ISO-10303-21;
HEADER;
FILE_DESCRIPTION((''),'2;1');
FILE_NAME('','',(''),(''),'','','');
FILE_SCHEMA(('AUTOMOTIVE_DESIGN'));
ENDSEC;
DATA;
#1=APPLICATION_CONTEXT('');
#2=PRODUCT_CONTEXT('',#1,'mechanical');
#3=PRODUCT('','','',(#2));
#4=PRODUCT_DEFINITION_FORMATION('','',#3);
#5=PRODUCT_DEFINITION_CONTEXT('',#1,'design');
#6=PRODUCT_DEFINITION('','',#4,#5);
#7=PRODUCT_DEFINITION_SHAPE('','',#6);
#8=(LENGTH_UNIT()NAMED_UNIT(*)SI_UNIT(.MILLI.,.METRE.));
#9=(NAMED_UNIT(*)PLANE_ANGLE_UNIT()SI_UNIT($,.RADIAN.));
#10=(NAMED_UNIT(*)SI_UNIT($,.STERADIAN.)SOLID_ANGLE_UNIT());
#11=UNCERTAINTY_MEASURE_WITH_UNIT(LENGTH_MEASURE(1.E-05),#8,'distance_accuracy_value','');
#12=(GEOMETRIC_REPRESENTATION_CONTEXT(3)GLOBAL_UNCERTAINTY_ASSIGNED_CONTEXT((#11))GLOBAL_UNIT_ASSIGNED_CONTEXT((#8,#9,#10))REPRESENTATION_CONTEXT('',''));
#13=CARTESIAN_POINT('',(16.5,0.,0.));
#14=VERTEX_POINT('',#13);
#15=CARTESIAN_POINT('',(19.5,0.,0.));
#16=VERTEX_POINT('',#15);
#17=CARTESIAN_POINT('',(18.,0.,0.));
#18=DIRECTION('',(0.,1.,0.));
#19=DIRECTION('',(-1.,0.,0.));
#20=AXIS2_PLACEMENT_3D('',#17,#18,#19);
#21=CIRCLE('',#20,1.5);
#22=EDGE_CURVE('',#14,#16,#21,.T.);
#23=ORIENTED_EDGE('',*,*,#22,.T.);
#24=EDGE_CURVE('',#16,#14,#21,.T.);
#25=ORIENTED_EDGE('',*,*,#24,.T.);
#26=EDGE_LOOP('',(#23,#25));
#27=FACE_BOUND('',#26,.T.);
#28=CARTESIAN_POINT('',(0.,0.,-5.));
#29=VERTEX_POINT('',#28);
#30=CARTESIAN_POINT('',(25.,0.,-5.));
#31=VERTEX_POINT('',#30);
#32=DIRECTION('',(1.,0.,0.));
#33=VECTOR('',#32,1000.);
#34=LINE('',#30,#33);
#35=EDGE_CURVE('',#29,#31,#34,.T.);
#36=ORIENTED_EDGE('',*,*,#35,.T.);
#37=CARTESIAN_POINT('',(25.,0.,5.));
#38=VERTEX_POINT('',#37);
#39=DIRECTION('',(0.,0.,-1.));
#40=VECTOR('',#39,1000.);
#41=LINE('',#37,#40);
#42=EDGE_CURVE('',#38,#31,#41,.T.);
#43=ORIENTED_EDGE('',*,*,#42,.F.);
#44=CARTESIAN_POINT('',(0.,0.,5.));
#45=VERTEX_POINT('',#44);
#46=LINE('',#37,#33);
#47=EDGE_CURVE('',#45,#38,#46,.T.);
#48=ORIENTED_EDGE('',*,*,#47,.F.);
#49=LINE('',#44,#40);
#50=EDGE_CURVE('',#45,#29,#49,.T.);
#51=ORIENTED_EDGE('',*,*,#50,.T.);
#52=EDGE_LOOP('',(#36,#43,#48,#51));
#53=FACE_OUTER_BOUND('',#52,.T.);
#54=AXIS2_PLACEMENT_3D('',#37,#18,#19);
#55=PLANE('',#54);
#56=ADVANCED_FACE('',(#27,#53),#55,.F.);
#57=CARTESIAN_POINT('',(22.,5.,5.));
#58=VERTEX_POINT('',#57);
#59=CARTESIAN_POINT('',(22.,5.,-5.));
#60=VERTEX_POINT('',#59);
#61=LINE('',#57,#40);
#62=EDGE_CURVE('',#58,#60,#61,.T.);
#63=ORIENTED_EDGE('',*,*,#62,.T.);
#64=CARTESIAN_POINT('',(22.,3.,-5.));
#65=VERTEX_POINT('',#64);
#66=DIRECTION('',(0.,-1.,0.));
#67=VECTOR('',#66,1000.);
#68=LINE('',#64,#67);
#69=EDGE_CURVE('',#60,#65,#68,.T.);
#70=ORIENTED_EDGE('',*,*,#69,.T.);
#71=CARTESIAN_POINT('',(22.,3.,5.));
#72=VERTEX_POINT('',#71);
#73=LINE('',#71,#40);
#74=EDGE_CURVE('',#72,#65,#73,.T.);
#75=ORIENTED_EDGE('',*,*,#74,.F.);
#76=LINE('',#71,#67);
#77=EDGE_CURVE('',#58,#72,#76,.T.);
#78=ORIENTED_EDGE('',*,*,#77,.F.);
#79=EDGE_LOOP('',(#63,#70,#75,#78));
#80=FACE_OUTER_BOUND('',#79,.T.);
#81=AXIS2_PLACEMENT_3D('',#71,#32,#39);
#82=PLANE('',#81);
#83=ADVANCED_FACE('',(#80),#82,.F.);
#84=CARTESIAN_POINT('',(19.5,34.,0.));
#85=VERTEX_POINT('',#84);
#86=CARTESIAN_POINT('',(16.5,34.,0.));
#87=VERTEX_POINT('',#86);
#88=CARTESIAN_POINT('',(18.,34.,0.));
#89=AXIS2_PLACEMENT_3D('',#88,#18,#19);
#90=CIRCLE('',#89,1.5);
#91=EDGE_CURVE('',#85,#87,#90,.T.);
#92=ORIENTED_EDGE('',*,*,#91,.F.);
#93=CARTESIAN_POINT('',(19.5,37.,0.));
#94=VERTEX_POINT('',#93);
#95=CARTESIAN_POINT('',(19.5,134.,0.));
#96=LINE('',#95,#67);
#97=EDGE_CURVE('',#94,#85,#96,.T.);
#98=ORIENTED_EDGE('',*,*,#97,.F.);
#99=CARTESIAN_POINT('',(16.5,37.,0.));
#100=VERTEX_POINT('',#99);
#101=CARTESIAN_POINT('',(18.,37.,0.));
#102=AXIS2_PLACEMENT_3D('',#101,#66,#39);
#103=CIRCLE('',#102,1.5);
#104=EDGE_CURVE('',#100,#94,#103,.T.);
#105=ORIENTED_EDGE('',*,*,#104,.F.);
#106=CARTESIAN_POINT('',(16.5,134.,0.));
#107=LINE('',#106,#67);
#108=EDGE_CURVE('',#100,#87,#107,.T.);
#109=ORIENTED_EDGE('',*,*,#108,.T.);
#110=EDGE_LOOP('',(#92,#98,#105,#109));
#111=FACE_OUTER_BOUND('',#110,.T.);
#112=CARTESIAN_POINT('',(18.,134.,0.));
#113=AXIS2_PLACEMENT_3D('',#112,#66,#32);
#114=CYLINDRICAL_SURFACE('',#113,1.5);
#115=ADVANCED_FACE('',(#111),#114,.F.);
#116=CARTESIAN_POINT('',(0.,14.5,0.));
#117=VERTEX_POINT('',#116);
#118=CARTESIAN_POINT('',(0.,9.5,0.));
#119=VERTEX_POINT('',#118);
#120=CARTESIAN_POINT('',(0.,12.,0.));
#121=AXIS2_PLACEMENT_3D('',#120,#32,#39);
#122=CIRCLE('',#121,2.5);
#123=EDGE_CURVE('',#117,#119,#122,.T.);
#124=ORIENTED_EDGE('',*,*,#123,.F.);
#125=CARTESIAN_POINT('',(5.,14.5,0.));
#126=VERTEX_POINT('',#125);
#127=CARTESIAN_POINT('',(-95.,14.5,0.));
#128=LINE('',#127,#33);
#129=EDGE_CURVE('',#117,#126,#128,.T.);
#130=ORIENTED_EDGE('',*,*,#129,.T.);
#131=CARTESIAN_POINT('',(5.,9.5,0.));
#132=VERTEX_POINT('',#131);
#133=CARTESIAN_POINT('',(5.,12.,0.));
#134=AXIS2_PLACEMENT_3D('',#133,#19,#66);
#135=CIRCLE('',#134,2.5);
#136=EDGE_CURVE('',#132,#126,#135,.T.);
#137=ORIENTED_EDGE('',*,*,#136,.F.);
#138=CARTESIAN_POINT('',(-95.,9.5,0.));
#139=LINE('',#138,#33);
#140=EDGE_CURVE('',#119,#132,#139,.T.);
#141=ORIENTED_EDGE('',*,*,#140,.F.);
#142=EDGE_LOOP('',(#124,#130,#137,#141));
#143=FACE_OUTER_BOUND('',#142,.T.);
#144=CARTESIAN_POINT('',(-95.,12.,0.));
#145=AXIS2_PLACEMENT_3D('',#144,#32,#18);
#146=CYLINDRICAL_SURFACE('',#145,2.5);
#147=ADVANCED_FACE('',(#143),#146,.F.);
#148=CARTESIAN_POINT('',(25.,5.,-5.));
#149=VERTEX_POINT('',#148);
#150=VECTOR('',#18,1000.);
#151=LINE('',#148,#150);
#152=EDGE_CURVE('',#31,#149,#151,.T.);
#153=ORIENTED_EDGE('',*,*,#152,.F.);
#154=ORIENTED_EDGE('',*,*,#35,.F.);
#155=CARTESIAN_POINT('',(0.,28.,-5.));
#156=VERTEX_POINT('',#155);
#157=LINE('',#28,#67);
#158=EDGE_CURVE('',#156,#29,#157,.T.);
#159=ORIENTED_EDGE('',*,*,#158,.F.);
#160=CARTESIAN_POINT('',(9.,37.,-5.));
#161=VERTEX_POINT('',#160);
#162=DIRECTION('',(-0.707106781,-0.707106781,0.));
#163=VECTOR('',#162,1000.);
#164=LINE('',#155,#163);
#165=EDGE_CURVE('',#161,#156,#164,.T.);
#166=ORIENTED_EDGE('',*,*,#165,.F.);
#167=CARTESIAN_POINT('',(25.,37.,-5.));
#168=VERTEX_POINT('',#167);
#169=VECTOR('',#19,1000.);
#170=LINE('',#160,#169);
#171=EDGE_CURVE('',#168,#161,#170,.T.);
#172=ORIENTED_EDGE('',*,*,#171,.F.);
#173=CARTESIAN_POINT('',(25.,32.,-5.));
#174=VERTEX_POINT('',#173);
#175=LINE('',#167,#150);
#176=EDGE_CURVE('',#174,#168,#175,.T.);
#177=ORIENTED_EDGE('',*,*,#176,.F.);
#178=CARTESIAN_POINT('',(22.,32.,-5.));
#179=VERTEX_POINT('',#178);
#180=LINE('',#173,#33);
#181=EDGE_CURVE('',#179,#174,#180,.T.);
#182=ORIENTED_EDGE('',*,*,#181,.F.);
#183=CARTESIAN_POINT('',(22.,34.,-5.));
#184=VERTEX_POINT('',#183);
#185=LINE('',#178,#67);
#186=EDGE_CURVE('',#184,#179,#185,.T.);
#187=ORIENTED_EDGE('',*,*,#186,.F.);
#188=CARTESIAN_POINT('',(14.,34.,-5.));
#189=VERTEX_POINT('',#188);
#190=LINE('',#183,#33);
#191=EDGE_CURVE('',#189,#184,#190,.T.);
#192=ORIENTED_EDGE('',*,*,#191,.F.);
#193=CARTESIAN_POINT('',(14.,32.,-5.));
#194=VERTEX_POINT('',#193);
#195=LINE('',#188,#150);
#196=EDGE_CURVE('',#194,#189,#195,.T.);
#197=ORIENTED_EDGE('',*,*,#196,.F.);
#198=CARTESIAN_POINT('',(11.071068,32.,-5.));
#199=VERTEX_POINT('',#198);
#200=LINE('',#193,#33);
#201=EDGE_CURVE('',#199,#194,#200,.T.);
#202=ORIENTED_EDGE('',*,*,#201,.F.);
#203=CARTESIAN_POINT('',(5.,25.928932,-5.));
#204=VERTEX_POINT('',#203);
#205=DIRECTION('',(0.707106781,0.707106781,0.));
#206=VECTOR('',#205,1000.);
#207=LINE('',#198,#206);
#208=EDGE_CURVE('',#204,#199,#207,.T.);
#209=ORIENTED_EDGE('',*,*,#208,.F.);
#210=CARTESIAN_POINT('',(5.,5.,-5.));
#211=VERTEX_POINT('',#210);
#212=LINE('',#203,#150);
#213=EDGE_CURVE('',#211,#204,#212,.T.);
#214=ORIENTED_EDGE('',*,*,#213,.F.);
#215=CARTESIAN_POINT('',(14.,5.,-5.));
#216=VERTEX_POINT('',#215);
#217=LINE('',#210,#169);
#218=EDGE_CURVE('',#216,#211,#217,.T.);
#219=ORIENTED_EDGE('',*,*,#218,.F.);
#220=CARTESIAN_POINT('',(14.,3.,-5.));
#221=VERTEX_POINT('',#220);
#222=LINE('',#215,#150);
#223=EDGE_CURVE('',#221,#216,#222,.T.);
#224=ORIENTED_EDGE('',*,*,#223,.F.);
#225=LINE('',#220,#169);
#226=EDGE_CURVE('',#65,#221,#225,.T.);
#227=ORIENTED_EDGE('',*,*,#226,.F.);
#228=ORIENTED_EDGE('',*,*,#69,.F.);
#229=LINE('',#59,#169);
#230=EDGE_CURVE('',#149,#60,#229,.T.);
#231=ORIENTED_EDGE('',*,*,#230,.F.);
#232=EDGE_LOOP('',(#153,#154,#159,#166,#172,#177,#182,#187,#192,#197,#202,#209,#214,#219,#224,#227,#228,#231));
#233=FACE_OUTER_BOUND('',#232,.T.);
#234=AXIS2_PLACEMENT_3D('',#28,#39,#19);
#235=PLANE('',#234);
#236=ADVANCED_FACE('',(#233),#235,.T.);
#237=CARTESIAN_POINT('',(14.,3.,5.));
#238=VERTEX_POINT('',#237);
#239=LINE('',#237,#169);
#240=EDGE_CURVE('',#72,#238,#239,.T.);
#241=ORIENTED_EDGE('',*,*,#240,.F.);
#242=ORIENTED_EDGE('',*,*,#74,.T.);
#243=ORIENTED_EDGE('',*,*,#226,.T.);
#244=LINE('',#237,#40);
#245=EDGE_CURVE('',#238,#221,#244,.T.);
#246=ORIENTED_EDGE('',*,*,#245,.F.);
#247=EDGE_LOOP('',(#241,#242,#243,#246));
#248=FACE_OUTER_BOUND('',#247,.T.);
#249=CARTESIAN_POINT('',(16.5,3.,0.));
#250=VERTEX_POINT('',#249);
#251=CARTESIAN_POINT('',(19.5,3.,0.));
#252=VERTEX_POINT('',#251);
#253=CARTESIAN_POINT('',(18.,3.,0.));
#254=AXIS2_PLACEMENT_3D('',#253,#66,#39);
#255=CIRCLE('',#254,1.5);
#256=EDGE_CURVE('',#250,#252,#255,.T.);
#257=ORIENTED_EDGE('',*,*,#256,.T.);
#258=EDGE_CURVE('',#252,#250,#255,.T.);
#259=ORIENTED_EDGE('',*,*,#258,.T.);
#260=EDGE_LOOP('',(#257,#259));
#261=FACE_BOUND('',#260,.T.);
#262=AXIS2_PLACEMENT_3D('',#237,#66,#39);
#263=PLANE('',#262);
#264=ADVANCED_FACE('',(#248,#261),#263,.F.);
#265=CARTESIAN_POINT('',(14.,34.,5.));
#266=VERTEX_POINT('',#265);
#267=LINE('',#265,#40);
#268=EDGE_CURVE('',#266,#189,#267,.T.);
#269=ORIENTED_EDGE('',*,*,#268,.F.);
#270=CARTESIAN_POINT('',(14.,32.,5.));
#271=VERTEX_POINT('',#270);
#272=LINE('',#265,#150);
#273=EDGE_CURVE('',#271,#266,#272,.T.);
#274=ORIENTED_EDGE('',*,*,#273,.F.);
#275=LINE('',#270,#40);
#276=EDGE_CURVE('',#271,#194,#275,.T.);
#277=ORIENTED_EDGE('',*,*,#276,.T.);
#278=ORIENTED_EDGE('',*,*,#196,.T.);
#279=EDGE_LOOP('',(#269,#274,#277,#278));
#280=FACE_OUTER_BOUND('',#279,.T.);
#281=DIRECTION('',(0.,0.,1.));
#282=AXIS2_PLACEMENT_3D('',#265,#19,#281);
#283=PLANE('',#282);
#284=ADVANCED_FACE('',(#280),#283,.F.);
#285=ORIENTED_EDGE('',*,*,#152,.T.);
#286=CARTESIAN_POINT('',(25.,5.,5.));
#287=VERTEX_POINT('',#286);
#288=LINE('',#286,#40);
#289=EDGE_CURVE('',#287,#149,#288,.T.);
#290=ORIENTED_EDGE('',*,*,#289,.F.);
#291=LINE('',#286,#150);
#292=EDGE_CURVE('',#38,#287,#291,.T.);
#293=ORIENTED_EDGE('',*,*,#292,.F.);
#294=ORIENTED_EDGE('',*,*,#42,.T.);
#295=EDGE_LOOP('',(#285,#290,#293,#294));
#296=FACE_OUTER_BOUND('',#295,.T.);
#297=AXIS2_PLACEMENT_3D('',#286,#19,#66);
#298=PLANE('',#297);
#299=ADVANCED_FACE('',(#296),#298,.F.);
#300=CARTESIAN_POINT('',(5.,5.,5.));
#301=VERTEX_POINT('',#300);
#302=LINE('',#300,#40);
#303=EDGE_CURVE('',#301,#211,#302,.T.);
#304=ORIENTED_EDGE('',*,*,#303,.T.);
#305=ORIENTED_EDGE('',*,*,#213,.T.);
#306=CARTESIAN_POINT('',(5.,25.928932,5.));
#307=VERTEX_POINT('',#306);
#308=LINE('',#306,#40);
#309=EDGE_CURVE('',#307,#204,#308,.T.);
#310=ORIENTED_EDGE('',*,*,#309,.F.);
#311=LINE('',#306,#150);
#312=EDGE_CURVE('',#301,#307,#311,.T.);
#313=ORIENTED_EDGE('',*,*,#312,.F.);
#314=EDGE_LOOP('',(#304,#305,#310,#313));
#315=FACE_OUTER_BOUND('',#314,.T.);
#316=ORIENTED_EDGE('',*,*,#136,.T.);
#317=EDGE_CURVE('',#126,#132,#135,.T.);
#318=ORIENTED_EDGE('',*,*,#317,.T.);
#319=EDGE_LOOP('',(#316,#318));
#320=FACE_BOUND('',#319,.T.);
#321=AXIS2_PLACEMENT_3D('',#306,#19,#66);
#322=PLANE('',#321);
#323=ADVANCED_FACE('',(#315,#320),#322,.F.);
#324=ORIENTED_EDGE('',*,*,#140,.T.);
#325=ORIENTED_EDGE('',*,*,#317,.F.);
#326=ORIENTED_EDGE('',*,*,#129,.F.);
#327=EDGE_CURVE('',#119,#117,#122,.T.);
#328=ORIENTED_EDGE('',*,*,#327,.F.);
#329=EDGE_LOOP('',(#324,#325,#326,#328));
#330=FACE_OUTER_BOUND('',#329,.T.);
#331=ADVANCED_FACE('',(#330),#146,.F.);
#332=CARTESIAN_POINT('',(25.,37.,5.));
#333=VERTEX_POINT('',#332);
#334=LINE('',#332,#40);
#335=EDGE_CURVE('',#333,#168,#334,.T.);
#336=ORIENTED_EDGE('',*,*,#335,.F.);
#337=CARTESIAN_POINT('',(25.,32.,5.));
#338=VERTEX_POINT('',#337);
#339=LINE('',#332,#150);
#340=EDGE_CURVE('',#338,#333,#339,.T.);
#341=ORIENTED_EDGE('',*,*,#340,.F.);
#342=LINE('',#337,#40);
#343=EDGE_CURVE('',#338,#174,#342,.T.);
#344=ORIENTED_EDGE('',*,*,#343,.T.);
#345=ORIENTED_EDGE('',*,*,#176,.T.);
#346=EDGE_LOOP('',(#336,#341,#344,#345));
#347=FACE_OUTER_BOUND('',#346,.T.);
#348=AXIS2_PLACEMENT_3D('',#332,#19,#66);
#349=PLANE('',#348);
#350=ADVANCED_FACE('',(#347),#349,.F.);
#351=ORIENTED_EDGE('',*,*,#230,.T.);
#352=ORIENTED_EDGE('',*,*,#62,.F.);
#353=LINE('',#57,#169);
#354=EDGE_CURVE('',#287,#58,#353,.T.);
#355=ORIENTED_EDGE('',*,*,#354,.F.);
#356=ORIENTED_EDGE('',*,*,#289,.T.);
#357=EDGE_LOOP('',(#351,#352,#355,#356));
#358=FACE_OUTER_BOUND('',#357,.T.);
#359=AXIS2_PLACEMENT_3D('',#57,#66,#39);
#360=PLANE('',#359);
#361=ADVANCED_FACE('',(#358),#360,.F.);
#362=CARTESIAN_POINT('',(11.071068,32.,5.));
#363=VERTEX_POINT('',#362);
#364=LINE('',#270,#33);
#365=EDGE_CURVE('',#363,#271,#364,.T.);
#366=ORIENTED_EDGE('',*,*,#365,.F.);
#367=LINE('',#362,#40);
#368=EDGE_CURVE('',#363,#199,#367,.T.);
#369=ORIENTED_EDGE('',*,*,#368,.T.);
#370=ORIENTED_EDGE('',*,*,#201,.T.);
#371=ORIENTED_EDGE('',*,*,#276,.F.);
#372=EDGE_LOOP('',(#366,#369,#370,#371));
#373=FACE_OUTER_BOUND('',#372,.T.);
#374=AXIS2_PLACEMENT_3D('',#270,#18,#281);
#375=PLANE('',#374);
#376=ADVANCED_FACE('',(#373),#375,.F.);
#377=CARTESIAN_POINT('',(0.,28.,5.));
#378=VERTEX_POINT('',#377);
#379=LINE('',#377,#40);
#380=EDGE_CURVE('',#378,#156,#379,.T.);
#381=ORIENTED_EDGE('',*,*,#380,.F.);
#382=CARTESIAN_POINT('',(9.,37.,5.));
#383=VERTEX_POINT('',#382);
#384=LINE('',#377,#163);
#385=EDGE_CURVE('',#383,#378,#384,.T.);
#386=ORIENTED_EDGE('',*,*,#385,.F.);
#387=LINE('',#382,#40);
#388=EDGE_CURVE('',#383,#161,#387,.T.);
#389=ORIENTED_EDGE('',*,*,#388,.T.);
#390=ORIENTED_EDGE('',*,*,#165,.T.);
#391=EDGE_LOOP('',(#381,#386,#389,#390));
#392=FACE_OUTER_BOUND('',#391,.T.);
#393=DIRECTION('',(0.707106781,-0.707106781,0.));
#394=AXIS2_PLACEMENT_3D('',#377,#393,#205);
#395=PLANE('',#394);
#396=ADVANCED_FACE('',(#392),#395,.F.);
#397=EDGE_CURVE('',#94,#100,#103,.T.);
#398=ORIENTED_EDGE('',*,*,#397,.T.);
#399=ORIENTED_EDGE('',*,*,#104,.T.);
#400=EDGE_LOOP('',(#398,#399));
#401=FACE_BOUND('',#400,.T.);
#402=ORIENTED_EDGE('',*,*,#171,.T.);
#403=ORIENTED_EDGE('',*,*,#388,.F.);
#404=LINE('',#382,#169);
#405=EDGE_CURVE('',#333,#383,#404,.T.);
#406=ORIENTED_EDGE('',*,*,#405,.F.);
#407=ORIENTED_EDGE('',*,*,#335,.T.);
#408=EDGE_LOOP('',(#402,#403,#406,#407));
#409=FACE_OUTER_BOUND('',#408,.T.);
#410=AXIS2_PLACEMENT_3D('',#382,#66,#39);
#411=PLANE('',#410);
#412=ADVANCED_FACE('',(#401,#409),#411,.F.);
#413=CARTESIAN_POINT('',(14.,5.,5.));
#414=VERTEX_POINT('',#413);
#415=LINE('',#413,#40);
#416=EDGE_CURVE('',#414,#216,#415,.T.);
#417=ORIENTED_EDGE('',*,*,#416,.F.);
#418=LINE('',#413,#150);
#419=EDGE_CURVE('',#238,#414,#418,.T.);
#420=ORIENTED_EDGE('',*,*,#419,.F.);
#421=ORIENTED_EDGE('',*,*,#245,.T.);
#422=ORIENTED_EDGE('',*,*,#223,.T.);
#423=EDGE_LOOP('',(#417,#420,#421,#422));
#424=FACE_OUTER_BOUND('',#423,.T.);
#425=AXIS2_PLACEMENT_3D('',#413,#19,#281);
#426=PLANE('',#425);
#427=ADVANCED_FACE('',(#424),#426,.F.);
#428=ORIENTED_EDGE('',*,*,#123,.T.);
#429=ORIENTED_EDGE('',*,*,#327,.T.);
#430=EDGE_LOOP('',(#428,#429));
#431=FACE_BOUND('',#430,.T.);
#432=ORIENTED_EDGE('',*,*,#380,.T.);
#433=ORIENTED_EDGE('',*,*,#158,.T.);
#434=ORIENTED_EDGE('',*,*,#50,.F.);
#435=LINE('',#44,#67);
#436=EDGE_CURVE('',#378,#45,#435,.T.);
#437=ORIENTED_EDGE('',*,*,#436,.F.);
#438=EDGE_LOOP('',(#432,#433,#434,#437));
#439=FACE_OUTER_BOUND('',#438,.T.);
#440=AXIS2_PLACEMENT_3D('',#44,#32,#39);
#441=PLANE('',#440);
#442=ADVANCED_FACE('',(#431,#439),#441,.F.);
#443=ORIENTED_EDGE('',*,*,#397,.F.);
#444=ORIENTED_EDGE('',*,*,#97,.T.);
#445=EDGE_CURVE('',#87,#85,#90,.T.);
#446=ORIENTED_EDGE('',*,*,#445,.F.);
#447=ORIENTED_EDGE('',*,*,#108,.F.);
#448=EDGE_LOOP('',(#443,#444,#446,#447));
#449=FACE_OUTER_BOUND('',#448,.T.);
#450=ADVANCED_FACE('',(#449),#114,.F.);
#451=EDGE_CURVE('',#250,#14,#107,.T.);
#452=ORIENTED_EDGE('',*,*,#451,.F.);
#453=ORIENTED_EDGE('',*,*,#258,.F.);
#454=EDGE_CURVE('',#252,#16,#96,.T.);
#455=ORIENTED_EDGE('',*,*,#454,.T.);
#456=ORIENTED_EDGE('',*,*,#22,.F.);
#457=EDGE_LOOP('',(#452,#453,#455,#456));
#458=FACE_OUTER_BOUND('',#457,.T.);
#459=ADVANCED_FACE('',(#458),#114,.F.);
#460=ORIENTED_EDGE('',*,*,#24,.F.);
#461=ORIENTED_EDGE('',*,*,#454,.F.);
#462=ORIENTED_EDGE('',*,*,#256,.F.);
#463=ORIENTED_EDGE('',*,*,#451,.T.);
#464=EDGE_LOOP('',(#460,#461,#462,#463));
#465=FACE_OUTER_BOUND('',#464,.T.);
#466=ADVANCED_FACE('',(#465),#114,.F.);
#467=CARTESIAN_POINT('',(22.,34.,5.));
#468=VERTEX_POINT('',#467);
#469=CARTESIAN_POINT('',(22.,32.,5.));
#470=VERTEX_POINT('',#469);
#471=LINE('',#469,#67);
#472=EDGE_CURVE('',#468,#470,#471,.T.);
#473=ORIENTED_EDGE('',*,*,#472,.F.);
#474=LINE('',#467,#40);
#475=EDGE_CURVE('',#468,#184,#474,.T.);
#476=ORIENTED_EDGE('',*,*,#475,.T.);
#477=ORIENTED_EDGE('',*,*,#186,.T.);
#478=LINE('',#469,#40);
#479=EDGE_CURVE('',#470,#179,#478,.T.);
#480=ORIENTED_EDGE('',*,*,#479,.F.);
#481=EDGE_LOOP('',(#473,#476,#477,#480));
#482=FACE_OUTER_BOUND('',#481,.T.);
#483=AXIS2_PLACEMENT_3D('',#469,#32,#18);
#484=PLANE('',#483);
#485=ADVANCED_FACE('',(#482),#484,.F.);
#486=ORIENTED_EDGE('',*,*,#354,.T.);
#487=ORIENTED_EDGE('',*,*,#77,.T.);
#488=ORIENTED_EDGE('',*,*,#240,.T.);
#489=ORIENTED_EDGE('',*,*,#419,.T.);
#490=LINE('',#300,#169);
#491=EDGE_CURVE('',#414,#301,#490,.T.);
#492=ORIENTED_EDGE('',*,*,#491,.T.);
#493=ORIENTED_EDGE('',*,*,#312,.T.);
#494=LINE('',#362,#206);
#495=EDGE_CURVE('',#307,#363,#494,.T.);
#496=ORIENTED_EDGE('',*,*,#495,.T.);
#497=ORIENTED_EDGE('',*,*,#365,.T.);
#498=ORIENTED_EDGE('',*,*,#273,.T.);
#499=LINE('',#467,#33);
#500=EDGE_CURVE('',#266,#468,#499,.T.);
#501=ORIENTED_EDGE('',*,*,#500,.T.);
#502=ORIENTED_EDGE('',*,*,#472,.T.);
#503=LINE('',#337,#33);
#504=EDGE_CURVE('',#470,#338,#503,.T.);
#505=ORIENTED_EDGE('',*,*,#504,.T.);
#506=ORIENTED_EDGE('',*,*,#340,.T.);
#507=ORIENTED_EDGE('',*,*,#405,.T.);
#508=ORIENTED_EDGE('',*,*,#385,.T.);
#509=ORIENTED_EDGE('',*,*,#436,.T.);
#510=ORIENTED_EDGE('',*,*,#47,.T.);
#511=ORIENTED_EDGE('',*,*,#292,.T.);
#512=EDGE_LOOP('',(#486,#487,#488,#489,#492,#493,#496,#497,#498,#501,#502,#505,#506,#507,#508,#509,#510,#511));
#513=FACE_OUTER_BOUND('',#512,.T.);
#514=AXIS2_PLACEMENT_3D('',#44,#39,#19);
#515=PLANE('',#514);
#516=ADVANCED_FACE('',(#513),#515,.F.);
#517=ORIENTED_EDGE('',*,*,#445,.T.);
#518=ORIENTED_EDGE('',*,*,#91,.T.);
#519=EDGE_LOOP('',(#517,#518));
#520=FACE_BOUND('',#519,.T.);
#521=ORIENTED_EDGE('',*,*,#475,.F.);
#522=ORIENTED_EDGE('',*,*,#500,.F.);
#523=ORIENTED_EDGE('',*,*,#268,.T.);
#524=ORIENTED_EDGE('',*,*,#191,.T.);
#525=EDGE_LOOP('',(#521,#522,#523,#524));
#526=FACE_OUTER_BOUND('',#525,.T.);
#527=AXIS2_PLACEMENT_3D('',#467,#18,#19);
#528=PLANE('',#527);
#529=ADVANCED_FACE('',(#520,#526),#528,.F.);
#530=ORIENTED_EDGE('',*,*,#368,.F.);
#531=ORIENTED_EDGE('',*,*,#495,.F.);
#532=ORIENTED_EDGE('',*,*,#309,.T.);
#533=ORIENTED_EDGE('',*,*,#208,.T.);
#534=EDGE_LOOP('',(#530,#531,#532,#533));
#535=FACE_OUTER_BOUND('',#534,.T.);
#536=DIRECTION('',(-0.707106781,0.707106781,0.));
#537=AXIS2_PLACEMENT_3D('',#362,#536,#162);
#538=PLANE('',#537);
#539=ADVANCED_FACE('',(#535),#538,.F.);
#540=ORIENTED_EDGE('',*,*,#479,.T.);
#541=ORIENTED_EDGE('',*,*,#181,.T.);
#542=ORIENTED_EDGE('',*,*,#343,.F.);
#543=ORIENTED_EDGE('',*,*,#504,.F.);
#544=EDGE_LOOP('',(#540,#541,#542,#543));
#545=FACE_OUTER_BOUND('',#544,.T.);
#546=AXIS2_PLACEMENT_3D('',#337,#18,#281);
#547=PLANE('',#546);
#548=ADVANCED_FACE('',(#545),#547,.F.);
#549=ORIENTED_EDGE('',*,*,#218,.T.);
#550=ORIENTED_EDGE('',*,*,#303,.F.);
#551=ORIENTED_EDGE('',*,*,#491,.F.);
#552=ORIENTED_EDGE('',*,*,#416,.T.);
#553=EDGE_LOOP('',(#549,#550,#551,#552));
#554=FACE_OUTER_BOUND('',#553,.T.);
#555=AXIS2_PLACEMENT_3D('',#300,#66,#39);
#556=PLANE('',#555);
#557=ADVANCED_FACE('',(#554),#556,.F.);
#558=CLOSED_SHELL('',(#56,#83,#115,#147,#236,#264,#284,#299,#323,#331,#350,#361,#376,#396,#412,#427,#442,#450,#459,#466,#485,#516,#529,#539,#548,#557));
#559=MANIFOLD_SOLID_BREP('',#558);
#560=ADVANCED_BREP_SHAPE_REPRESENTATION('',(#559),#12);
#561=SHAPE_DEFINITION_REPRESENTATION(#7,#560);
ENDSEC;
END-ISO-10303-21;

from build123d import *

# Parameters (mm, degrees)
C_BRACKET_BODY_DEPTH = 5
FLANGE_HOLE_SKETCH_R = 1.5
FLANGE_HOLES_3_DEPTH = 100
WEB_HOLE_SKETCH_R    = 2.5
WEB_HOLE_DEPTH       = 100


with BuildPart() as part:
    # C Profile Sketch → C Bracket Body (new, symmetric)
    with BuildSketch(Plane.XY):
        Polygon((0, 0), (0, 28), (9, 37), (25, 37), (25, 32), (22, 32), (22, 34), (14, 34), (14, 32), (11.071067812, 32), (5, 25.928932188), (5, 5), (14, 5), (14, 3), (22, 3), (22, 5), (25, 5), (25, 0), align=None)
    extrude(amount=C_BRACKET_BODY_DEPTH, both=True)

    # Flange Hole Sketch → Flange Holes Ø3 (cut, symmetric)
    with BuildSketch(Plane.XZ.offset(-34)):
        with Locations(Location((18, 0, 0), (0, 0, 270))):
            Circle(FLANGE_HOLE_SKETCH_R)
    extrude(amount=FLANGE_HOLES_3_DEPTH, both=True, mode=Mode.SUBTRACT)

    # Web Hole Sketch → Web Hole (cut, symmetric)
    with BuildSketch(Plane(origin=(5, 0, 0), x_dir=(0, 0, -1), z_dir=(1, 0, 0))):
        with Locations((0, 12)):
            Circle(WEB_HOLE_SKETCH_R)
    extrude(amount=WEB_HOLE_DEPTH, both=True, mode=Mode.SUBTRACT)


solid = part.part
